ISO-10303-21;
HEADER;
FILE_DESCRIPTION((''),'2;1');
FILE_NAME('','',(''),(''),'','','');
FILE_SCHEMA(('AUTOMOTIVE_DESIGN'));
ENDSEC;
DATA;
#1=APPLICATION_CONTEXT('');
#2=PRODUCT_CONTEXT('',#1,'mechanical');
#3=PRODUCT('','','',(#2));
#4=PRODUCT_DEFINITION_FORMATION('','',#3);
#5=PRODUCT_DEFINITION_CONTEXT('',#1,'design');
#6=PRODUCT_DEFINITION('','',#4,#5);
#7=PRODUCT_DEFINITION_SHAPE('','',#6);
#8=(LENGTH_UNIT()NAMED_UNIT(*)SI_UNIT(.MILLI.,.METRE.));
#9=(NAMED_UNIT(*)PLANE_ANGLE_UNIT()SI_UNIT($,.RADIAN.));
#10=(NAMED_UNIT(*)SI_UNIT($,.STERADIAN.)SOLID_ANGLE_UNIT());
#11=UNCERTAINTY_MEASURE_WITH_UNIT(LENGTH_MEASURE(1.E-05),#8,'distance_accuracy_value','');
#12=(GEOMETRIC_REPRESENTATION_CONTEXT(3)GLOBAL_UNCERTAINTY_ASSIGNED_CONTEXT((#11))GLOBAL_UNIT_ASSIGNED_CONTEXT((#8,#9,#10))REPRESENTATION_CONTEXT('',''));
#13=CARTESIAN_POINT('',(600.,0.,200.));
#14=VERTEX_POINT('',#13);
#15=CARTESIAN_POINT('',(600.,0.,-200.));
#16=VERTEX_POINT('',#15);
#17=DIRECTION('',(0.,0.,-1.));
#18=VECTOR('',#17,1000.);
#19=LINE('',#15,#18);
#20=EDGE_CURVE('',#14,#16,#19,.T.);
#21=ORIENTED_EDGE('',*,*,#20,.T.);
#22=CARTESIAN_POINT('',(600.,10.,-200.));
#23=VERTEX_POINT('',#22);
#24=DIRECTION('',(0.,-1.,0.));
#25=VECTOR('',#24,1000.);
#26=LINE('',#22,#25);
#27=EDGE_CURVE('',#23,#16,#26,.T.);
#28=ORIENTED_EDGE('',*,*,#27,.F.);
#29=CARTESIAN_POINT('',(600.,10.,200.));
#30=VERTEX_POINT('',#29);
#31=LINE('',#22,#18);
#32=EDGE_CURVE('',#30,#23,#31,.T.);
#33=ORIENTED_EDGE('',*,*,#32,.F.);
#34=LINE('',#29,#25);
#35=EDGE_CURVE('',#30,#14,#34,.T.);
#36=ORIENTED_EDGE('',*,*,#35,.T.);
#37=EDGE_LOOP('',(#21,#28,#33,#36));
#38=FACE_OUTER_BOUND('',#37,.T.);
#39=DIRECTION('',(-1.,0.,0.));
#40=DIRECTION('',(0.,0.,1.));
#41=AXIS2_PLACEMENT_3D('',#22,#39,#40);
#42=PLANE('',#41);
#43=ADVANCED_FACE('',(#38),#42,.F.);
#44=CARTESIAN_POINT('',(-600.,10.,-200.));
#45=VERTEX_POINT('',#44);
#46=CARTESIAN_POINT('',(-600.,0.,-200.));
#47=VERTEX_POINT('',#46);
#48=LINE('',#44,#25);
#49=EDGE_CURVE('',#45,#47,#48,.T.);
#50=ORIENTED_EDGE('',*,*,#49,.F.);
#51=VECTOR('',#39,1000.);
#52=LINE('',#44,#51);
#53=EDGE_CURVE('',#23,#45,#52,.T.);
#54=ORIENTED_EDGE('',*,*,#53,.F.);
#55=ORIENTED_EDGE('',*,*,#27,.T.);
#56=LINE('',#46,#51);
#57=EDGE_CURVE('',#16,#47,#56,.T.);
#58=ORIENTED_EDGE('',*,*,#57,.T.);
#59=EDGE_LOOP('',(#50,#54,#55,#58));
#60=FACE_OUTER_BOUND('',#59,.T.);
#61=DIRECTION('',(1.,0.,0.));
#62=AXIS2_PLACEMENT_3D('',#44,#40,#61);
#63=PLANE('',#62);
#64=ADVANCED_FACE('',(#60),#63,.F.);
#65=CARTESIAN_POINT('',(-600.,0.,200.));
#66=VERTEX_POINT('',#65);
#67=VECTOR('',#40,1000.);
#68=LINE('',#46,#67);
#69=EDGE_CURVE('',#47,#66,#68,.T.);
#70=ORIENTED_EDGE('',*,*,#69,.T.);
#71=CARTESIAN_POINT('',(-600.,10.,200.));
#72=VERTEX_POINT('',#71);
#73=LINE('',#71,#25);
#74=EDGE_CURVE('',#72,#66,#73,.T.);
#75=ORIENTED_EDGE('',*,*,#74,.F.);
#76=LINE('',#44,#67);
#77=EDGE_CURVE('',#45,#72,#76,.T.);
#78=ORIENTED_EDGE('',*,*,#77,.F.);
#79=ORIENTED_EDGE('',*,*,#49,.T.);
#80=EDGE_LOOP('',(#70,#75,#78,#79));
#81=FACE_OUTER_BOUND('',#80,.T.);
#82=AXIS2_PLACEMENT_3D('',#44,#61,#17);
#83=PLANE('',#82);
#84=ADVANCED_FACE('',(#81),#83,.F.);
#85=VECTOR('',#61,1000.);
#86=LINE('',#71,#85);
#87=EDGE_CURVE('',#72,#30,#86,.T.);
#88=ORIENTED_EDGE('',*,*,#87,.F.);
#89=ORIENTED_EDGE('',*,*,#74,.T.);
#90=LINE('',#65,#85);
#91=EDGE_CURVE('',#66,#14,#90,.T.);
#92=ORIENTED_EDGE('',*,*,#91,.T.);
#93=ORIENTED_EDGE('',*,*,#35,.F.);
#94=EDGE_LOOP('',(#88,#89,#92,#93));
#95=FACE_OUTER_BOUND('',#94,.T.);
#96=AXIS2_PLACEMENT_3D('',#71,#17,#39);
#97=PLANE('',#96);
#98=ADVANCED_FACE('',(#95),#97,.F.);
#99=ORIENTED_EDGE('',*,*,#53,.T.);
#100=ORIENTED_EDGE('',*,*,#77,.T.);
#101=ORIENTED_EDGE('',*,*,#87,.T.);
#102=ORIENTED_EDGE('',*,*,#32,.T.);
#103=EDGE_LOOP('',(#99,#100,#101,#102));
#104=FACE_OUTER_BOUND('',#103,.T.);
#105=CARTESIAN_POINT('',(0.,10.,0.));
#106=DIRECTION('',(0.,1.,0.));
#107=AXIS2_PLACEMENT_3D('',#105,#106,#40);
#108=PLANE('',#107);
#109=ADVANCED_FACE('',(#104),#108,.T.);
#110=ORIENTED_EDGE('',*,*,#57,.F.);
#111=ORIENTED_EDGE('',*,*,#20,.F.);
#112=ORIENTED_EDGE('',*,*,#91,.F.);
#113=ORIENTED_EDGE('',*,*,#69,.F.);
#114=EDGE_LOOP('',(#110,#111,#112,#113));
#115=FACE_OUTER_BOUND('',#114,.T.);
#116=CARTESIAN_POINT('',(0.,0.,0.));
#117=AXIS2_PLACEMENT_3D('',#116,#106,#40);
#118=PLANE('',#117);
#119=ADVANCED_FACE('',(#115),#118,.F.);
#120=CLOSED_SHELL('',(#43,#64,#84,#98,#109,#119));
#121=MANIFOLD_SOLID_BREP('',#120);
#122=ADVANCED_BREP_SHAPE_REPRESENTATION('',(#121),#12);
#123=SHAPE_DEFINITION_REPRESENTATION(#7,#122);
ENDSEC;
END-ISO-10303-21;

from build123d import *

# Parameters (mm, degrees)
SKETCH1_W           = 1200
SKETCH1_H           = 400
BOSS_EXTRUDE1_DEPTH = 10


with BuildPart() as part:
    # Sketch1 → Boss-Extrude1 (new body)
    with BuildSketch(Plane(origin=(0, 0, 0), x_dir=(1, 0, 0), z_dir=(0, 1, 0))):
        Rectangle(SKETCH1_W, SKETCH1_H)
    extrude(amount=BOSS_EXTRUDE1_DEPTH)


solid = part.part
